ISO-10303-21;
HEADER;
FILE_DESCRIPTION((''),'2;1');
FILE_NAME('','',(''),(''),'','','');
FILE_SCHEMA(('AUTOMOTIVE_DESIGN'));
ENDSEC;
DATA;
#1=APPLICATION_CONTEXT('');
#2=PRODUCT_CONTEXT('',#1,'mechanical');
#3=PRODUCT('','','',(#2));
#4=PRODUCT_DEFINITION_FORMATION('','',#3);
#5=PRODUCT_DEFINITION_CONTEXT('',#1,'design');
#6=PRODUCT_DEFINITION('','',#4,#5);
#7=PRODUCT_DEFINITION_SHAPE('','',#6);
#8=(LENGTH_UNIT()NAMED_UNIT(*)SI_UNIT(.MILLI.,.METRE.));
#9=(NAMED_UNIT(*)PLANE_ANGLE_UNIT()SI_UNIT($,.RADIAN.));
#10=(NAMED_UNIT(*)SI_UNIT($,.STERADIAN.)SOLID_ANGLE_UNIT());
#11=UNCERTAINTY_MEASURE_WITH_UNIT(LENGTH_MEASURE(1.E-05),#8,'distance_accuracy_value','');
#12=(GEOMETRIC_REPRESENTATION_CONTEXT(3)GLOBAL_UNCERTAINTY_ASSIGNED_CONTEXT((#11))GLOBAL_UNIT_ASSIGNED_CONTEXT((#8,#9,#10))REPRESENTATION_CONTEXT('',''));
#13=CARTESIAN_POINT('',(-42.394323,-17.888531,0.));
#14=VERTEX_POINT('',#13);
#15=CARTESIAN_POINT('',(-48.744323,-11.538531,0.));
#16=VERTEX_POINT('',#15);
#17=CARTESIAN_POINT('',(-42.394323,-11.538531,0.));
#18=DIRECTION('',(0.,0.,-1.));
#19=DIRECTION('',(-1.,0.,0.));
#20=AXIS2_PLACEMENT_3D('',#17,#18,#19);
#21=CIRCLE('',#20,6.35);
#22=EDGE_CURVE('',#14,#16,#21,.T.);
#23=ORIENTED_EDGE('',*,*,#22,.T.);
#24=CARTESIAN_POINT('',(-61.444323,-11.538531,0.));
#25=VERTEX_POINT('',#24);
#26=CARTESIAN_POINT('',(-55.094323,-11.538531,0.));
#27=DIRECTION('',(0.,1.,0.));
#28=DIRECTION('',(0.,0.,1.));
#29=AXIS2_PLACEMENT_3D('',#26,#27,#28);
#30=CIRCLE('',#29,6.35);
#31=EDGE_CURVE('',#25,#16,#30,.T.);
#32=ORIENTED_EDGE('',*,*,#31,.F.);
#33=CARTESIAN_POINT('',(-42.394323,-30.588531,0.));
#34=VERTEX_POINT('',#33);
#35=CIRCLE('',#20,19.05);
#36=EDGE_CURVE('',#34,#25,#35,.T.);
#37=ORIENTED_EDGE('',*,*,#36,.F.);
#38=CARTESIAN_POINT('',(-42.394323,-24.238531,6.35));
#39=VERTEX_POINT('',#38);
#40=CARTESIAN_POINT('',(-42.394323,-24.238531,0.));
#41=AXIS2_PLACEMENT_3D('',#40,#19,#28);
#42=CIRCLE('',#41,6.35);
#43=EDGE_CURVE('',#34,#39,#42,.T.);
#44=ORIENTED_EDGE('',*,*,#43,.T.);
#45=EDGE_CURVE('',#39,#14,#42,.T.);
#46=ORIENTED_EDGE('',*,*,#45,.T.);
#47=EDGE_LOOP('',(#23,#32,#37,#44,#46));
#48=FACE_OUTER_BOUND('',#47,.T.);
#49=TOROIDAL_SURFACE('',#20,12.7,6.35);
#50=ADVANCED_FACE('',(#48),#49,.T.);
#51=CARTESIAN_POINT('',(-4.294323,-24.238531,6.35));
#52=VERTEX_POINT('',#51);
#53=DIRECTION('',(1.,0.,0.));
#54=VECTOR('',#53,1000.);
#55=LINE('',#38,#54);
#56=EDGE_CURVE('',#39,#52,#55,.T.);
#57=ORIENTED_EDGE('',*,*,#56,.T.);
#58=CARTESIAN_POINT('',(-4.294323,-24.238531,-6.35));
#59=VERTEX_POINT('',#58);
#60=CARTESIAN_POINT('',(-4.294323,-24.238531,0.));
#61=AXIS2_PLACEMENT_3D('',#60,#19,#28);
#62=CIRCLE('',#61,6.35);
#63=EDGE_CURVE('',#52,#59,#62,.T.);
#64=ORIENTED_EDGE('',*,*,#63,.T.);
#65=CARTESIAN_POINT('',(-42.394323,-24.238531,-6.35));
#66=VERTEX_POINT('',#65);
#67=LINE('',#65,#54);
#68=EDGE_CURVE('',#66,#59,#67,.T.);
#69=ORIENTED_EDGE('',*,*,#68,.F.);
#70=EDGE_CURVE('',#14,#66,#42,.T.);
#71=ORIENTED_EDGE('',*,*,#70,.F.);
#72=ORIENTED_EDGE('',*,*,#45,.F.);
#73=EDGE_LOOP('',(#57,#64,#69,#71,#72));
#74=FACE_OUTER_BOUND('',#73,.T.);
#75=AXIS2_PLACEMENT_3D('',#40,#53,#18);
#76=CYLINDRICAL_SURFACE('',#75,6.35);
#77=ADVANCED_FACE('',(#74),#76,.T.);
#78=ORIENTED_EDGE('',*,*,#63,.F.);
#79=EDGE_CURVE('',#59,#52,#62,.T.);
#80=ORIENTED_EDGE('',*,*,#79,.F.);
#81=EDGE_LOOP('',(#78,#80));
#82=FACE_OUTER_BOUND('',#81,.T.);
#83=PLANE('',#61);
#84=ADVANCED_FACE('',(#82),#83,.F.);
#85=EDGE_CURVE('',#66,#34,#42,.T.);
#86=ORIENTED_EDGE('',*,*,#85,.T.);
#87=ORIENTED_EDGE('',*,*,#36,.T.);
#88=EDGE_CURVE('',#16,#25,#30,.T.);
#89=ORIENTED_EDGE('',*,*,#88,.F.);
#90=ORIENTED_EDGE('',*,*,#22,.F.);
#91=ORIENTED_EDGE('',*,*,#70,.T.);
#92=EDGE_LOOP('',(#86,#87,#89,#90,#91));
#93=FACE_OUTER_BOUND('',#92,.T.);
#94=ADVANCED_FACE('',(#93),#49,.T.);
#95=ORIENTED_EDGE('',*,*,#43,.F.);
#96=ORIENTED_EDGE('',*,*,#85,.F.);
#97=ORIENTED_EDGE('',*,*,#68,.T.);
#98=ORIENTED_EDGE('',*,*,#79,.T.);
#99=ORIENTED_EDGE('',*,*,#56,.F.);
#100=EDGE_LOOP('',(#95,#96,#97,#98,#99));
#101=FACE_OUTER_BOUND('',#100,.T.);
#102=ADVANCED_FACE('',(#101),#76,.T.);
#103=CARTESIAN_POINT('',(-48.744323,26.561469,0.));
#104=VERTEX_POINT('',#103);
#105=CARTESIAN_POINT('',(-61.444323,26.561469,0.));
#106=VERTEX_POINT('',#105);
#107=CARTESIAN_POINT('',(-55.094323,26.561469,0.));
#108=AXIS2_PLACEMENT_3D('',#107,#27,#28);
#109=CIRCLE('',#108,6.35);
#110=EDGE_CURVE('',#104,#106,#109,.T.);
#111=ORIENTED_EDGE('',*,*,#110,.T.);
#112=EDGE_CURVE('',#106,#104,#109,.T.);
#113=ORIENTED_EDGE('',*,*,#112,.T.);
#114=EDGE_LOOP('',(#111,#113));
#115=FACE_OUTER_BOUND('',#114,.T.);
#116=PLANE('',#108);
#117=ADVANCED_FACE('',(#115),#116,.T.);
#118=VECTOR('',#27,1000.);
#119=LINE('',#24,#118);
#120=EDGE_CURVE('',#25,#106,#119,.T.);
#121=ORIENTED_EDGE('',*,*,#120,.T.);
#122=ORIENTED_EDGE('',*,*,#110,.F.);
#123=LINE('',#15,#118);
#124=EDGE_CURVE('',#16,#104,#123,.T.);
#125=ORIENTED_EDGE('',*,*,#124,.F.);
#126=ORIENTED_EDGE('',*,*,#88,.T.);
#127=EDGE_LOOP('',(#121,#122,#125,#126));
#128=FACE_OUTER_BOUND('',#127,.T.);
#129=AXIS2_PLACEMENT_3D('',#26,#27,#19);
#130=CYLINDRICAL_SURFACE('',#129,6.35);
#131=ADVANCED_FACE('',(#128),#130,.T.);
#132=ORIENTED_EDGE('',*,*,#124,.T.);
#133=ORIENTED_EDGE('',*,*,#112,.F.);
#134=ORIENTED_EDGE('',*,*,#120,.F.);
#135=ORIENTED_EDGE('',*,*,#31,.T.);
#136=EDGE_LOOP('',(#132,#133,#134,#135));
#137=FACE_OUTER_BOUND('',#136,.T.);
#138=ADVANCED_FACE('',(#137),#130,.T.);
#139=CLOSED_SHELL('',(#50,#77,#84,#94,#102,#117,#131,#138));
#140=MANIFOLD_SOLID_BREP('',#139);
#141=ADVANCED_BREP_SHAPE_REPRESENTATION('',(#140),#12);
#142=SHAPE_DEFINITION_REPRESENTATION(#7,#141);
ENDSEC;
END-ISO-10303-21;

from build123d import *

# Parameters (mm, degrees)
SKETCH2_R = 6.35


with BuildPart() as part:
    # Sweep8: sweep along a path in Sketch1
    with BuildLine(Plane.XY) as sweep8_path:
        Line((-4.294322906, -24.238530735), (-42.394322906, -24.238530735))
        ThreePointArc((-42.394322906, -24.238530735), (-51.374579027, -20.518786856), (-55.094322906, -11.538530735))
        Line((-55.094322906, -11.538530735), (-55.094322906, 26.561469265))
    # Sketch2 → Sweep8 (sweep)
    with BuildSketch(Plane.ZY.offset(4.294322906)):
        with Locations((0, -24.238530735)):
            Circle(SKETCH2_R)
    sweep(path=sweep8_path.line)


solid = part.part
